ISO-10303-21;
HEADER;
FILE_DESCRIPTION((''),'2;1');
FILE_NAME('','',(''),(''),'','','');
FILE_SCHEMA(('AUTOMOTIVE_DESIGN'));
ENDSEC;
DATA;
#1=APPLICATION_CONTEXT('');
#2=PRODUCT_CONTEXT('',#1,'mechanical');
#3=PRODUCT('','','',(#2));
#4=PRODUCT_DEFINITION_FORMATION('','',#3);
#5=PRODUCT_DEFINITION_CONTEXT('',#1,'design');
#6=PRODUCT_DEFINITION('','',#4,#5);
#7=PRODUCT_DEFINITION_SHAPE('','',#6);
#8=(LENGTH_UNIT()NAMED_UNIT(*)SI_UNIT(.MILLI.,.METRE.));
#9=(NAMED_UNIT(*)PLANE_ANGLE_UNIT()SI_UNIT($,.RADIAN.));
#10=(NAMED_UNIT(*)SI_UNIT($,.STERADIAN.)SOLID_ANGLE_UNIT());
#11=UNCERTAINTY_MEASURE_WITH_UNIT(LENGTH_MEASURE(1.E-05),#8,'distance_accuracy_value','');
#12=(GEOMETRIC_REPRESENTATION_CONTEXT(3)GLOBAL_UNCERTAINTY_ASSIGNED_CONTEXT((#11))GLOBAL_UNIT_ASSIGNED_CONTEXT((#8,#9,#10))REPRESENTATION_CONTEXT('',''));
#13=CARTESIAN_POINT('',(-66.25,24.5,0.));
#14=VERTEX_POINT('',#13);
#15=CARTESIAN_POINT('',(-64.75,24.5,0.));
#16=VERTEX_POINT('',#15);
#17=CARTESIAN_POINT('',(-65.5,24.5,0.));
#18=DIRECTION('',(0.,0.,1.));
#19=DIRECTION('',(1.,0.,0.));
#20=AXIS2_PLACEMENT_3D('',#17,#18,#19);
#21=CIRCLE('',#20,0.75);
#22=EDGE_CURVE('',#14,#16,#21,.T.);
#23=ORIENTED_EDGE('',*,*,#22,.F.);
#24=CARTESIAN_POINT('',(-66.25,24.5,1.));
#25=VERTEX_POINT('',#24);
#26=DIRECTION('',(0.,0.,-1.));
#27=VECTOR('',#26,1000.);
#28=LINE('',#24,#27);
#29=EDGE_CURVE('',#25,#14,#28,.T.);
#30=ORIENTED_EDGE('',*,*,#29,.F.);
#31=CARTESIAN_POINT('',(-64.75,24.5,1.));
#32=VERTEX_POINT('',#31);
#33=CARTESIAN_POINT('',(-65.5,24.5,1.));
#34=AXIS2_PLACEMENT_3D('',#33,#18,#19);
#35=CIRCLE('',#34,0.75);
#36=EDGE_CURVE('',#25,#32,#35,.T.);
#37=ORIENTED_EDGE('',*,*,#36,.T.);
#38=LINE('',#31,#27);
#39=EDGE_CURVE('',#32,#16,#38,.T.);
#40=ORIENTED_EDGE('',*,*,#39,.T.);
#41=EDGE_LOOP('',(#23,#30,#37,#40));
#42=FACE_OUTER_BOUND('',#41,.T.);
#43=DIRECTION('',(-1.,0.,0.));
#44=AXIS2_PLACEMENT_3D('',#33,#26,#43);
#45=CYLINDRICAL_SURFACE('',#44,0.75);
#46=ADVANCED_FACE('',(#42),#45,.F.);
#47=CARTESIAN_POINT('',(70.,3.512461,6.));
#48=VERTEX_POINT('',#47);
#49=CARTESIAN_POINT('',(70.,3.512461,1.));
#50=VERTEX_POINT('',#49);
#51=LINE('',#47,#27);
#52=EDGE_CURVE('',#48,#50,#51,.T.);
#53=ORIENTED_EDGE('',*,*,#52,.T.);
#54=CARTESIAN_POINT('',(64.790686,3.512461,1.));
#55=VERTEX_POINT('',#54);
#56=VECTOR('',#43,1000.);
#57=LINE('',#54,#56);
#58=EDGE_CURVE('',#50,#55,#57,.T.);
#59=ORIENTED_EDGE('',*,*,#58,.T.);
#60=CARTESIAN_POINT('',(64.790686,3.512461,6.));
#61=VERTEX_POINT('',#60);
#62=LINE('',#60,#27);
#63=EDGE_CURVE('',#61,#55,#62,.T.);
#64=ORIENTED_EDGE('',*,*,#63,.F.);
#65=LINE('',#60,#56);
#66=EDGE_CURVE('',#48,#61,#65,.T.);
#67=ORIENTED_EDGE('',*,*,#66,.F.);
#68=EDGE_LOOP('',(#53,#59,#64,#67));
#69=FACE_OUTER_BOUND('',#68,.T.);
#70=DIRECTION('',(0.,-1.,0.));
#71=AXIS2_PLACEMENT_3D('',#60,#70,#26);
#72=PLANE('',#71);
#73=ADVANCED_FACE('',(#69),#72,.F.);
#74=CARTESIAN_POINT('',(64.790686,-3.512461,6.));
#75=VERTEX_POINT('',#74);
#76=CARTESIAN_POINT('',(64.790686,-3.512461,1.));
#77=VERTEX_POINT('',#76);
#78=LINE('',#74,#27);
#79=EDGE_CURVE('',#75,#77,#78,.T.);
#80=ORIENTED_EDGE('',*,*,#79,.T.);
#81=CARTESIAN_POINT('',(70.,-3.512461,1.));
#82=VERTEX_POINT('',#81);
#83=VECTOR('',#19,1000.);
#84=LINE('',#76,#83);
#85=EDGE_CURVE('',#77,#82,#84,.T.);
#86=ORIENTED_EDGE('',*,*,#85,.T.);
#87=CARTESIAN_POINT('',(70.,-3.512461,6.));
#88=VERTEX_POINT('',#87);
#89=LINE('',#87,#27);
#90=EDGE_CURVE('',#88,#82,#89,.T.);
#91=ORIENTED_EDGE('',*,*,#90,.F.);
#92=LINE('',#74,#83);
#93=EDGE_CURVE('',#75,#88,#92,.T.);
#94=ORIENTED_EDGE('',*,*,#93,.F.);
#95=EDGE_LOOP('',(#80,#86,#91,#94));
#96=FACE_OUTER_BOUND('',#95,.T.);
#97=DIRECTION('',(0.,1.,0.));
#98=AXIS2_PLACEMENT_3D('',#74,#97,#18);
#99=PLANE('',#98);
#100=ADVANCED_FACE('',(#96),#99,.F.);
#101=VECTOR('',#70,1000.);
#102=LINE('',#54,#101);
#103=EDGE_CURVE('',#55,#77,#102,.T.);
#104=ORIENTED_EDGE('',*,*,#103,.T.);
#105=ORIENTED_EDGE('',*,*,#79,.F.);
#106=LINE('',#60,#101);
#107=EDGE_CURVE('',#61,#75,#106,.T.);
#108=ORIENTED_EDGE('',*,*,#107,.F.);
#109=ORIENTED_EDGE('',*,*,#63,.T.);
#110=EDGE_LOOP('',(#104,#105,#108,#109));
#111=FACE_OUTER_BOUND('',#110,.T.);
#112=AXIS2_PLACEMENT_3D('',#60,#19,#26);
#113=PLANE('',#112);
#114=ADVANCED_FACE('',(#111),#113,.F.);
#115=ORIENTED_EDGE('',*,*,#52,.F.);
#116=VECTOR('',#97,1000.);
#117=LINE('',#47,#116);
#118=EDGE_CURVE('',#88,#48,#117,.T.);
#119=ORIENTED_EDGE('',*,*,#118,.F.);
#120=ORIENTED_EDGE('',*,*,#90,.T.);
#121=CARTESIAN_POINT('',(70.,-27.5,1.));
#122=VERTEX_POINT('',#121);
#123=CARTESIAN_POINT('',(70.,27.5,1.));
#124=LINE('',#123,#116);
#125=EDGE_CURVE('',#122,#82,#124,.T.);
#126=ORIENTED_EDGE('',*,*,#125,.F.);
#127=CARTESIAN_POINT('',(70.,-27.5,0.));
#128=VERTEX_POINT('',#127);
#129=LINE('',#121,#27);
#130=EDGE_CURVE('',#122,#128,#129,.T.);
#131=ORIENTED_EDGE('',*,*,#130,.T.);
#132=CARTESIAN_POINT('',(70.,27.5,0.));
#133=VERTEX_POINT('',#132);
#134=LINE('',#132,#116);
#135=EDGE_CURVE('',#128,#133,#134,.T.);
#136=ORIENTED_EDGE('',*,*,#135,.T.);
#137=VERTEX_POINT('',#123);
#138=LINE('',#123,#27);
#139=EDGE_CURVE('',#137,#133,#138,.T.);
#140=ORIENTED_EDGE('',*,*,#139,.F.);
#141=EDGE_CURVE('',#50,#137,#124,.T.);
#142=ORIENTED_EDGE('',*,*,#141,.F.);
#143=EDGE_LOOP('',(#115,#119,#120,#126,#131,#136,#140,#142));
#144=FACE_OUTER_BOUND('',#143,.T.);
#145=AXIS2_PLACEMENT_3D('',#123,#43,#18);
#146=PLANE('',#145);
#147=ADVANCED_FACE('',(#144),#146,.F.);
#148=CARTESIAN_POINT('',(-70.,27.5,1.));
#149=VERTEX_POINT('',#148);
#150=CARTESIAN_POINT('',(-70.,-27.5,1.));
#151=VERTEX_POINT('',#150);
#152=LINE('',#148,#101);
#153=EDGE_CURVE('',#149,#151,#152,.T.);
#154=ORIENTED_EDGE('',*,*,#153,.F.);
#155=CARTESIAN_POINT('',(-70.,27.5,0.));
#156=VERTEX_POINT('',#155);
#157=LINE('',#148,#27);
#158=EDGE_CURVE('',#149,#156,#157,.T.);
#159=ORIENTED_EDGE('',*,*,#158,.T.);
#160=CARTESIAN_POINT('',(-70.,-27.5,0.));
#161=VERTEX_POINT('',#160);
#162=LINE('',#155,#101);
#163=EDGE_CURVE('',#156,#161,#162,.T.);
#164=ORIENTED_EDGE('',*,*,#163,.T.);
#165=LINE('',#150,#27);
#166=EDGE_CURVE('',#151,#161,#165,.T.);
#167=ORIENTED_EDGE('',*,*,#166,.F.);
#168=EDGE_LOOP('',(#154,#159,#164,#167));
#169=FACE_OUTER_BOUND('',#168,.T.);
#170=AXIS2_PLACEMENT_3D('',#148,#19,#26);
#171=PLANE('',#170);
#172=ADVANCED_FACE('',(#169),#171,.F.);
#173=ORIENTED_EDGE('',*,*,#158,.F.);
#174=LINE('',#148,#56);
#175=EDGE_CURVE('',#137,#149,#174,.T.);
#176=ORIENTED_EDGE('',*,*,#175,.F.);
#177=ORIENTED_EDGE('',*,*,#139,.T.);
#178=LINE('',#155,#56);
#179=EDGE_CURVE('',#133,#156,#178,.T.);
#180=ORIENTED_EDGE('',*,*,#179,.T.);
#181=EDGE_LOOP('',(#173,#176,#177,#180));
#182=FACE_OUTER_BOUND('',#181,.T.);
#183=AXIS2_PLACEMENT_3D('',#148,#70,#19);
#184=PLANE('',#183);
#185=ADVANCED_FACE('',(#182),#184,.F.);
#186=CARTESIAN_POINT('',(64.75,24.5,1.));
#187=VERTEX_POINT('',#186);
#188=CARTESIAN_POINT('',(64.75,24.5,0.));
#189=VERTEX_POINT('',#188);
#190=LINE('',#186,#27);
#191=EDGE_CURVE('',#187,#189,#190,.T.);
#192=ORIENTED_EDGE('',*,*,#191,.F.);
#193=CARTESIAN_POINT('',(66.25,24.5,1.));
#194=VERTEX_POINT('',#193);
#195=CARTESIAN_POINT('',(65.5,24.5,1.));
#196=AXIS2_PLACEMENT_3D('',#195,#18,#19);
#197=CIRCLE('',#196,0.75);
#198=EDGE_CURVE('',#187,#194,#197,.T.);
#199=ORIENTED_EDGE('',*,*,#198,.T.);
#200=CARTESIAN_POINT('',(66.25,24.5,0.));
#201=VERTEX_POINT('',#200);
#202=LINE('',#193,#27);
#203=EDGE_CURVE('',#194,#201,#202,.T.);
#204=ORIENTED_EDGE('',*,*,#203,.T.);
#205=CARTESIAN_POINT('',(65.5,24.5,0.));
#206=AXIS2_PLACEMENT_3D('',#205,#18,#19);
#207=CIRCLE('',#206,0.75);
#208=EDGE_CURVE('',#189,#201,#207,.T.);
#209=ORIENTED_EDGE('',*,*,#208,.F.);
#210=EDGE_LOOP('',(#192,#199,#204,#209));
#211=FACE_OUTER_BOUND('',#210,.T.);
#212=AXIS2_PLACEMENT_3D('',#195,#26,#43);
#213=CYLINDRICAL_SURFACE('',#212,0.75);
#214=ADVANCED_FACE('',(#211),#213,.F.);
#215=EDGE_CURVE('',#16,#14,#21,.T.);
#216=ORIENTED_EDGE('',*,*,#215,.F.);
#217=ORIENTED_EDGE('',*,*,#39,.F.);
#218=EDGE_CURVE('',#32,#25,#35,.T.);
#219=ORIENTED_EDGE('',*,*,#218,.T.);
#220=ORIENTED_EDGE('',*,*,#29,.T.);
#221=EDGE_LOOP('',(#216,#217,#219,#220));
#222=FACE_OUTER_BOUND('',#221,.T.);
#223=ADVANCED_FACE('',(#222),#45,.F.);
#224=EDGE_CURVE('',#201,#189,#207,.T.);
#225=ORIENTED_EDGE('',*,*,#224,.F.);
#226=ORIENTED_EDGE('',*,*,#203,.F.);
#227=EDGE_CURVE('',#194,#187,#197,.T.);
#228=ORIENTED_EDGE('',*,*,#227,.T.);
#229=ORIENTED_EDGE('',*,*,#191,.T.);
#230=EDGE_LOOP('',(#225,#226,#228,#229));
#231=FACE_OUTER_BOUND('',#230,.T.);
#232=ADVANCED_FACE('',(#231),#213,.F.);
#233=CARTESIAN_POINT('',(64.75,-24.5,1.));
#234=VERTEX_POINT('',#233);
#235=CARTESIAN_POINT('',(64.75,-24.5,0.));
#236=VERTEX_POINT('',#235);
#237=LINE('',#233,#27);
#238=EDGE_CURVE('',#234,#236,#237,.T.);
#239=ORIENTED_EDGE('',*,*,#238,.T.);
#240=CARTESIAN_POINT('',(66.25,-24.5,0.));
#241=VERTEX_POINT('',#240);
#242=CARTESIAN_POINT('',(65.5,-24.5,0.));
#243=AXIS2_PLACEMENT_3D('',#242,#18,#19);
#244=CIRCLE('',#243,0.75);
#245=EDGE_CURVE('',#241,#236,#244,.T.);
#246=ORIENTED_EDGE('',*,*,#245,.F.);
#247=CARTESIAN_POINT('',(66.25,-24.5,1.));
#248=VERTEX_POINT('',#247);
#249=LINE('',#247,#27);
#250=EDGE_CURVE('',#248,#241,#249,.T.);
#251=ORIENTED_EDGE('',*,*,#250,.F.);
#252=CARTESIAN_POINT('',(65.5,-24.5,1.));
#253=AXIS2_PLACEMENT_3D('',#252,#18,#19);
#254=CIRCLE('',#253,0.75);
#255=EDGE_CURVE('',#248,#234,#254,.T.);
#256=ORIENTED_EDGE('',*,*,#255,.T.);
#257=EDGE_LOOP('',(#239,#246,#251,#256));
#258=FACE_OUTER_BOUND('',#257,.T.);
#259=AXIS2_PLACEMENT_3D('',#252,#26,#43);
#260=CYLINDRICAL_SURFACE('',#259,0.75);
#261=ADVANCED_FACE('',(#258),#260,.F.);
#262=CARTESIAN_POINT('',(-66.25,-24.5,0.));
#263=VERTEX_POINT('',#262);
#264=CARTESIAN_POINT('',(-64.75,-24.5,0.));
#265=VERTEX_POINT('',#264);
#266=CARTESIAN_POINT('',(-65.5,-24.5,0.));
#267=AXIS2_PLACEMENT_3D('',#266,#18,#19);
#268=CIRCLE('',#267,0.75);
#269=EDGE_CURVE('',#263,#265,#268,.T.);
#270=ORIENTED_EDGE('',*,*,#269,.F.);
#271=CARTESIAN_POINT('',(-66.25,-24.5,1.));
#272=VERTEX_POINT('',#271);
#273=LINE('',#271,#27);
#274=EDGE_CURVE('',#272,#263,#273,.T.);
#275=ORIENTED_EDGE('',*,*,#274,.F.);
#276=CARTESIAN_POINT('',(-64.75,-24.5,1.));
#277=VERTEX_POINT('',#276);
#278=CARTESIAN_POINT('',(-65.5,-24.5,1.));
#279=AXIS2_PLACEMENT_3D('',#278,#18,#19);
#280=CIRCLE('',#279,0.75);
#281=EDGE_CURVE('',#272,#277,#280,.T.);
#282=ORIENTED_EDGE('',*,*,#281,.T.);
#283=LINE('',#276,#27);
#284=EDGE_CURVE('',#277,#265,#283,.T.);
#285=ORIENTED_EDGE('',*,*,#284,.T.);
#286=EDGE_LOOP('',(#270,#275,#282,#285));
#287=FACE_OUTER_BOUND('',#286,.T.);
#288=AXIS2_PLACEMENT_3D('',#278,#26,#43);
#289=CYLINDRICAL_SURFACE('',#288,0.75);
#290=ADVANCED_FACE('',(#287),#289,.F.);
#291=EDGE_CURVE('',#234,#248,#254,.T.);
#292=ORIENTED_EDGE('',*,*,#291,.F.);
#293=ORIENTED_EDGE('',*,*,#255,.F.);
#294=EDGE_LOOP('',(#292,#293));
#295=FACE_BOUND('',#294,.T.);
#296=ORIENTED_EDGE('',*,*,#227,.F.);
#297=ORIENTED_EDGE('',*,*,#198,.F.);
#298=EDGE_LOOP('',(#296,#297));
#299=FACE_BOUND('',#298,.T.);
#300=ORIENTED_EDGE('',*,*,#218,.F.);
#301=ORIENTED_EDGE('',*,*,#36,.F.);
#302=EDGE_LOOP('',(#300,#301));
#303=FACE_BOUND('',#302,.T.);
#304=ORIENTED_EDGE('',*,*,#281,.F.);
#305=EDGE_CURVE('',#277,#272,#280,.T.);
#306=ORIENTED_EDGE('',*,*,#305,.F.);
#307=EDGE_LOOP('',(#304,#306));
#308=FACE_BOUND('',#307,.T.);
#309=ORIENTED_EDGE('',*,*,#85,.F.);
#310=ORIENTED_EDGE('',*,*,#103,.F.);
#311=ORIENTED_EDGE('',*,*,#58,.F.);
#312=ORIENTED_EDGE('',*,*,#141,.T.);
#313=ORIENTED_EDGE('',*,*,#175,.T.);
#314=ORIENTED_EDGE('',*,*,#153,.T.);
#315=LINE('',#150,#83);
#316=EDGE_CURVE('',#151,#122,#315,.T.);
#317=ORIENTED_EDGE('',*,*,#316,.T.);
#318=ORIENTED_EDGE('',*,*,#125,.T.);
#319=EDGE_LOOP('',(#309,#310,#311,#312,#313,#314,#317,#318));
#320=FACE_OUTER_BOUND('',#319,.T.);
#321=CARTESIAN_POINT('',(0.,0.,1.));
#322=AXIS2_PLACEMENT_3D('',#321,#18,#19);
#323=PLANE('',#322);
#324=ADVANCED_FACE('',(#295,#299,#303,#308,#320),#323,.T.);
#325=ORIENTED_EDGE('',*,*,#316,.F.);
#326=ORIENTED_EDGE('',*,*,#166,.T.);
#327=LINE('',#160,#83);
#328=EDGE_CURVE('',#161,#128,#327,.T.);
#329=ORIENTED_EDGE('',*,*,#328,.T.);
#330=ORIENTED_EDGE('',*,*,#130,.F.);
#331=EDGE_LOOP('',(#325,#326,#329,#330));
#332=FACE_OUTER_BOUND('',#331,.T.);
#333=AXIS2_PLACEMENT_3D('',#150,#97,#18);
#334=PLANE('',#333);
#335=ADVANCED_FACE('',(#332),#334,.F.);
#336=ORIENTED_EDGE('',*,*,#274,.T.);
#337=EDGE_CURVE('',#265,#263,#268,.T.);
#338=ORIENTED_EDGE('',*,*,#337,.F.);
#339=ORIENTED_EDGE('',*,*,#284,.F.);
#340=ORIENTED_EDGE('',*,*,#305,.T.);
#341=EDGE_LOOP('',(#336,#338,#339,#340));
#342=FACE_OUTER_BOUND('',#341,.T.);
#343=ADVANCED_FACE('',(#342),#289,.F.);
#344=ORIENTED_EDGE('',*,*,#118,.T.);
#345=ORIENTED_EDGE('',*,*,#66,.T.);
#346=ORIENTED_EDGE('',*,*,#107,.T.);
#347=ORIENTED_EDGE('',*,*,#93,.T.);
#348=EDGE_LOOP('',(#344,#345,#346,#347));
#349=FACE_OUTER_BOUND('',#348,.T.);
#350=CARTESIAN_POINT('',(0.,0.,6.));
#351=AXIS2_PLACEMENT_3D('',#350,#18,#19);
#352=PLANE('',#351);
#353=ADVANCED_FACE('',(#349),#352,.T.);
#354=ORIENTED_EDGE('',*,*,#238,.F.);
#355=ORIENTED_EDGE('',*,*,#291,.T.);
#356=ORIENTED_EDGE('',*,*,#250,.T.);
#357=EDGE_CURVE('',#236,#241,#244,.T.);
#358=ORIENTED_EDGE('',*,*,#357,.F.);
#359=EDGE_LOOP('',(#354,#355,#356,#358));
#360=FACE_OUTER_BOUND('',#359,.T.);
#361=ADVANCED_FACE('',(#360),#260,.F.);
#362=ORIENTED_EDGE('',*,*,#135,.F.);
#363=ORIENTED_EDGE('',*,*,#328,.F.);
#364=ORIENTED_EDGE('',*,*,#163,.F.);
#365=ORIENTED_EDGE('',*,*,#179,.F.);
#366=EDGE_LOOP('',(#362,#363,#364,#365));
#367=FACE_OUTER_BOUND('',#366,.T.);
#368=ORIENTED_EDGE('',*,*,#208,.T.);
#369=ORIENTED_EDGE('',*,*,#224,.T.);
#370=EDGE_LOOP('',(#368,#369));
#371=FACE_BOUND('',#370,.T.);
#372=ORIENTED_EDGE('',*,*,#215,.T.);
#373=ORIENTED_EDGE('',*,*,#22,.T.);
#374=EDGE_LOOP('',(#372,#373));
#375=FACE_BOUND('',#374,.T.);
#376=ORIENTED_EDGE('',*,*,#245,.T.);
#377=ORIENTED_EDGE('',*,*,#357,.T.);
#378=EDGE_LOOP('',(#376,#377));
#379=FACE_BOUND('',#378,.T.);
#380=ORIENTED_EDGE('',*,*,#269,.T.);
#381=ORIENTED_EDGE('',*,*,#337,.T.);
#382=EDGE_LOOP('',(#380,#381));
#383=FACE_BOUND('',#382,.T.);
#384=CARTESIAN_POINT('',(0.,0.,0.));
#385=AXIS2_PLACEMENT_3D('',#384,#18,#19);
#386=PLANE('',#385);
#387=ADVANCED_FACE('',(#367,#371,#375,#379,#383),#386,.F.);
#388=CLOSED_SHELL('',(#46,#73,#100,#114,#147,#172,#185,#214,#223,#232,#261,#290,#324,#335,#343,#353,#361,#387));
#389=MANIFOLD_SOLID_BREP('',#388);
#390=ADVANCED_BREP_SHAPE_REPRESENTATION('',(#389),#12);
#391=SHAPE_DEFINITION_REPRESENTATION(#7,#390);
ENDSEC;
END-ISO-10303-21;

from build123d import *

# Parameters (mm, degrees)
SKETCH1_W           = 140
SKETCH1_H           = 55
SKETCH1_R           = 0.75
BOSS_EXTRUDE1_DEPTH = 1
SKETCH2_W           = 5.209314299
SKETCH2_H           = 7.02492173
BOSS_EXTRUDE2_DEPTH = 5


with BuildPart() as part:
    # Sketch1 → Boss-Extrude1 (new body)
    with BuildSketch(Plane.XY):
        Rectangle(SKETCH1_W, SKETCH1_H)
        with Locations((-65.5, -24.5)):
            Circle(SKETCH1_R, mode=Mode.SUBTRACT)
        with Locations((-65.5, 24.5)):
            Circle(SKETCH1_R, mode=Mode.SUBTRACT)
        with Locations((65.5, 24.5)):
            Circle(SKETCH1_R, mode=Mode.SUBTRACT)
        with Locations((65.5, -24.5)):
            Circle(SKETCH1_R, mode=Mode.SUBTRACT)
    extrude(amount=BOSS_EXTRUDE1_DEPTH)

    # Sketch2 → Boss-Extrude2 (add)
    with BuildSketch(Plane.XY.offset(1)):
        with Locations((67.395342851, 0)):
            Rectangle(SKETCH2_W, SKETCH2_H)
    extrude(amount=BOSS_EXTRUDE2_DEPTH)


solid = part.part
